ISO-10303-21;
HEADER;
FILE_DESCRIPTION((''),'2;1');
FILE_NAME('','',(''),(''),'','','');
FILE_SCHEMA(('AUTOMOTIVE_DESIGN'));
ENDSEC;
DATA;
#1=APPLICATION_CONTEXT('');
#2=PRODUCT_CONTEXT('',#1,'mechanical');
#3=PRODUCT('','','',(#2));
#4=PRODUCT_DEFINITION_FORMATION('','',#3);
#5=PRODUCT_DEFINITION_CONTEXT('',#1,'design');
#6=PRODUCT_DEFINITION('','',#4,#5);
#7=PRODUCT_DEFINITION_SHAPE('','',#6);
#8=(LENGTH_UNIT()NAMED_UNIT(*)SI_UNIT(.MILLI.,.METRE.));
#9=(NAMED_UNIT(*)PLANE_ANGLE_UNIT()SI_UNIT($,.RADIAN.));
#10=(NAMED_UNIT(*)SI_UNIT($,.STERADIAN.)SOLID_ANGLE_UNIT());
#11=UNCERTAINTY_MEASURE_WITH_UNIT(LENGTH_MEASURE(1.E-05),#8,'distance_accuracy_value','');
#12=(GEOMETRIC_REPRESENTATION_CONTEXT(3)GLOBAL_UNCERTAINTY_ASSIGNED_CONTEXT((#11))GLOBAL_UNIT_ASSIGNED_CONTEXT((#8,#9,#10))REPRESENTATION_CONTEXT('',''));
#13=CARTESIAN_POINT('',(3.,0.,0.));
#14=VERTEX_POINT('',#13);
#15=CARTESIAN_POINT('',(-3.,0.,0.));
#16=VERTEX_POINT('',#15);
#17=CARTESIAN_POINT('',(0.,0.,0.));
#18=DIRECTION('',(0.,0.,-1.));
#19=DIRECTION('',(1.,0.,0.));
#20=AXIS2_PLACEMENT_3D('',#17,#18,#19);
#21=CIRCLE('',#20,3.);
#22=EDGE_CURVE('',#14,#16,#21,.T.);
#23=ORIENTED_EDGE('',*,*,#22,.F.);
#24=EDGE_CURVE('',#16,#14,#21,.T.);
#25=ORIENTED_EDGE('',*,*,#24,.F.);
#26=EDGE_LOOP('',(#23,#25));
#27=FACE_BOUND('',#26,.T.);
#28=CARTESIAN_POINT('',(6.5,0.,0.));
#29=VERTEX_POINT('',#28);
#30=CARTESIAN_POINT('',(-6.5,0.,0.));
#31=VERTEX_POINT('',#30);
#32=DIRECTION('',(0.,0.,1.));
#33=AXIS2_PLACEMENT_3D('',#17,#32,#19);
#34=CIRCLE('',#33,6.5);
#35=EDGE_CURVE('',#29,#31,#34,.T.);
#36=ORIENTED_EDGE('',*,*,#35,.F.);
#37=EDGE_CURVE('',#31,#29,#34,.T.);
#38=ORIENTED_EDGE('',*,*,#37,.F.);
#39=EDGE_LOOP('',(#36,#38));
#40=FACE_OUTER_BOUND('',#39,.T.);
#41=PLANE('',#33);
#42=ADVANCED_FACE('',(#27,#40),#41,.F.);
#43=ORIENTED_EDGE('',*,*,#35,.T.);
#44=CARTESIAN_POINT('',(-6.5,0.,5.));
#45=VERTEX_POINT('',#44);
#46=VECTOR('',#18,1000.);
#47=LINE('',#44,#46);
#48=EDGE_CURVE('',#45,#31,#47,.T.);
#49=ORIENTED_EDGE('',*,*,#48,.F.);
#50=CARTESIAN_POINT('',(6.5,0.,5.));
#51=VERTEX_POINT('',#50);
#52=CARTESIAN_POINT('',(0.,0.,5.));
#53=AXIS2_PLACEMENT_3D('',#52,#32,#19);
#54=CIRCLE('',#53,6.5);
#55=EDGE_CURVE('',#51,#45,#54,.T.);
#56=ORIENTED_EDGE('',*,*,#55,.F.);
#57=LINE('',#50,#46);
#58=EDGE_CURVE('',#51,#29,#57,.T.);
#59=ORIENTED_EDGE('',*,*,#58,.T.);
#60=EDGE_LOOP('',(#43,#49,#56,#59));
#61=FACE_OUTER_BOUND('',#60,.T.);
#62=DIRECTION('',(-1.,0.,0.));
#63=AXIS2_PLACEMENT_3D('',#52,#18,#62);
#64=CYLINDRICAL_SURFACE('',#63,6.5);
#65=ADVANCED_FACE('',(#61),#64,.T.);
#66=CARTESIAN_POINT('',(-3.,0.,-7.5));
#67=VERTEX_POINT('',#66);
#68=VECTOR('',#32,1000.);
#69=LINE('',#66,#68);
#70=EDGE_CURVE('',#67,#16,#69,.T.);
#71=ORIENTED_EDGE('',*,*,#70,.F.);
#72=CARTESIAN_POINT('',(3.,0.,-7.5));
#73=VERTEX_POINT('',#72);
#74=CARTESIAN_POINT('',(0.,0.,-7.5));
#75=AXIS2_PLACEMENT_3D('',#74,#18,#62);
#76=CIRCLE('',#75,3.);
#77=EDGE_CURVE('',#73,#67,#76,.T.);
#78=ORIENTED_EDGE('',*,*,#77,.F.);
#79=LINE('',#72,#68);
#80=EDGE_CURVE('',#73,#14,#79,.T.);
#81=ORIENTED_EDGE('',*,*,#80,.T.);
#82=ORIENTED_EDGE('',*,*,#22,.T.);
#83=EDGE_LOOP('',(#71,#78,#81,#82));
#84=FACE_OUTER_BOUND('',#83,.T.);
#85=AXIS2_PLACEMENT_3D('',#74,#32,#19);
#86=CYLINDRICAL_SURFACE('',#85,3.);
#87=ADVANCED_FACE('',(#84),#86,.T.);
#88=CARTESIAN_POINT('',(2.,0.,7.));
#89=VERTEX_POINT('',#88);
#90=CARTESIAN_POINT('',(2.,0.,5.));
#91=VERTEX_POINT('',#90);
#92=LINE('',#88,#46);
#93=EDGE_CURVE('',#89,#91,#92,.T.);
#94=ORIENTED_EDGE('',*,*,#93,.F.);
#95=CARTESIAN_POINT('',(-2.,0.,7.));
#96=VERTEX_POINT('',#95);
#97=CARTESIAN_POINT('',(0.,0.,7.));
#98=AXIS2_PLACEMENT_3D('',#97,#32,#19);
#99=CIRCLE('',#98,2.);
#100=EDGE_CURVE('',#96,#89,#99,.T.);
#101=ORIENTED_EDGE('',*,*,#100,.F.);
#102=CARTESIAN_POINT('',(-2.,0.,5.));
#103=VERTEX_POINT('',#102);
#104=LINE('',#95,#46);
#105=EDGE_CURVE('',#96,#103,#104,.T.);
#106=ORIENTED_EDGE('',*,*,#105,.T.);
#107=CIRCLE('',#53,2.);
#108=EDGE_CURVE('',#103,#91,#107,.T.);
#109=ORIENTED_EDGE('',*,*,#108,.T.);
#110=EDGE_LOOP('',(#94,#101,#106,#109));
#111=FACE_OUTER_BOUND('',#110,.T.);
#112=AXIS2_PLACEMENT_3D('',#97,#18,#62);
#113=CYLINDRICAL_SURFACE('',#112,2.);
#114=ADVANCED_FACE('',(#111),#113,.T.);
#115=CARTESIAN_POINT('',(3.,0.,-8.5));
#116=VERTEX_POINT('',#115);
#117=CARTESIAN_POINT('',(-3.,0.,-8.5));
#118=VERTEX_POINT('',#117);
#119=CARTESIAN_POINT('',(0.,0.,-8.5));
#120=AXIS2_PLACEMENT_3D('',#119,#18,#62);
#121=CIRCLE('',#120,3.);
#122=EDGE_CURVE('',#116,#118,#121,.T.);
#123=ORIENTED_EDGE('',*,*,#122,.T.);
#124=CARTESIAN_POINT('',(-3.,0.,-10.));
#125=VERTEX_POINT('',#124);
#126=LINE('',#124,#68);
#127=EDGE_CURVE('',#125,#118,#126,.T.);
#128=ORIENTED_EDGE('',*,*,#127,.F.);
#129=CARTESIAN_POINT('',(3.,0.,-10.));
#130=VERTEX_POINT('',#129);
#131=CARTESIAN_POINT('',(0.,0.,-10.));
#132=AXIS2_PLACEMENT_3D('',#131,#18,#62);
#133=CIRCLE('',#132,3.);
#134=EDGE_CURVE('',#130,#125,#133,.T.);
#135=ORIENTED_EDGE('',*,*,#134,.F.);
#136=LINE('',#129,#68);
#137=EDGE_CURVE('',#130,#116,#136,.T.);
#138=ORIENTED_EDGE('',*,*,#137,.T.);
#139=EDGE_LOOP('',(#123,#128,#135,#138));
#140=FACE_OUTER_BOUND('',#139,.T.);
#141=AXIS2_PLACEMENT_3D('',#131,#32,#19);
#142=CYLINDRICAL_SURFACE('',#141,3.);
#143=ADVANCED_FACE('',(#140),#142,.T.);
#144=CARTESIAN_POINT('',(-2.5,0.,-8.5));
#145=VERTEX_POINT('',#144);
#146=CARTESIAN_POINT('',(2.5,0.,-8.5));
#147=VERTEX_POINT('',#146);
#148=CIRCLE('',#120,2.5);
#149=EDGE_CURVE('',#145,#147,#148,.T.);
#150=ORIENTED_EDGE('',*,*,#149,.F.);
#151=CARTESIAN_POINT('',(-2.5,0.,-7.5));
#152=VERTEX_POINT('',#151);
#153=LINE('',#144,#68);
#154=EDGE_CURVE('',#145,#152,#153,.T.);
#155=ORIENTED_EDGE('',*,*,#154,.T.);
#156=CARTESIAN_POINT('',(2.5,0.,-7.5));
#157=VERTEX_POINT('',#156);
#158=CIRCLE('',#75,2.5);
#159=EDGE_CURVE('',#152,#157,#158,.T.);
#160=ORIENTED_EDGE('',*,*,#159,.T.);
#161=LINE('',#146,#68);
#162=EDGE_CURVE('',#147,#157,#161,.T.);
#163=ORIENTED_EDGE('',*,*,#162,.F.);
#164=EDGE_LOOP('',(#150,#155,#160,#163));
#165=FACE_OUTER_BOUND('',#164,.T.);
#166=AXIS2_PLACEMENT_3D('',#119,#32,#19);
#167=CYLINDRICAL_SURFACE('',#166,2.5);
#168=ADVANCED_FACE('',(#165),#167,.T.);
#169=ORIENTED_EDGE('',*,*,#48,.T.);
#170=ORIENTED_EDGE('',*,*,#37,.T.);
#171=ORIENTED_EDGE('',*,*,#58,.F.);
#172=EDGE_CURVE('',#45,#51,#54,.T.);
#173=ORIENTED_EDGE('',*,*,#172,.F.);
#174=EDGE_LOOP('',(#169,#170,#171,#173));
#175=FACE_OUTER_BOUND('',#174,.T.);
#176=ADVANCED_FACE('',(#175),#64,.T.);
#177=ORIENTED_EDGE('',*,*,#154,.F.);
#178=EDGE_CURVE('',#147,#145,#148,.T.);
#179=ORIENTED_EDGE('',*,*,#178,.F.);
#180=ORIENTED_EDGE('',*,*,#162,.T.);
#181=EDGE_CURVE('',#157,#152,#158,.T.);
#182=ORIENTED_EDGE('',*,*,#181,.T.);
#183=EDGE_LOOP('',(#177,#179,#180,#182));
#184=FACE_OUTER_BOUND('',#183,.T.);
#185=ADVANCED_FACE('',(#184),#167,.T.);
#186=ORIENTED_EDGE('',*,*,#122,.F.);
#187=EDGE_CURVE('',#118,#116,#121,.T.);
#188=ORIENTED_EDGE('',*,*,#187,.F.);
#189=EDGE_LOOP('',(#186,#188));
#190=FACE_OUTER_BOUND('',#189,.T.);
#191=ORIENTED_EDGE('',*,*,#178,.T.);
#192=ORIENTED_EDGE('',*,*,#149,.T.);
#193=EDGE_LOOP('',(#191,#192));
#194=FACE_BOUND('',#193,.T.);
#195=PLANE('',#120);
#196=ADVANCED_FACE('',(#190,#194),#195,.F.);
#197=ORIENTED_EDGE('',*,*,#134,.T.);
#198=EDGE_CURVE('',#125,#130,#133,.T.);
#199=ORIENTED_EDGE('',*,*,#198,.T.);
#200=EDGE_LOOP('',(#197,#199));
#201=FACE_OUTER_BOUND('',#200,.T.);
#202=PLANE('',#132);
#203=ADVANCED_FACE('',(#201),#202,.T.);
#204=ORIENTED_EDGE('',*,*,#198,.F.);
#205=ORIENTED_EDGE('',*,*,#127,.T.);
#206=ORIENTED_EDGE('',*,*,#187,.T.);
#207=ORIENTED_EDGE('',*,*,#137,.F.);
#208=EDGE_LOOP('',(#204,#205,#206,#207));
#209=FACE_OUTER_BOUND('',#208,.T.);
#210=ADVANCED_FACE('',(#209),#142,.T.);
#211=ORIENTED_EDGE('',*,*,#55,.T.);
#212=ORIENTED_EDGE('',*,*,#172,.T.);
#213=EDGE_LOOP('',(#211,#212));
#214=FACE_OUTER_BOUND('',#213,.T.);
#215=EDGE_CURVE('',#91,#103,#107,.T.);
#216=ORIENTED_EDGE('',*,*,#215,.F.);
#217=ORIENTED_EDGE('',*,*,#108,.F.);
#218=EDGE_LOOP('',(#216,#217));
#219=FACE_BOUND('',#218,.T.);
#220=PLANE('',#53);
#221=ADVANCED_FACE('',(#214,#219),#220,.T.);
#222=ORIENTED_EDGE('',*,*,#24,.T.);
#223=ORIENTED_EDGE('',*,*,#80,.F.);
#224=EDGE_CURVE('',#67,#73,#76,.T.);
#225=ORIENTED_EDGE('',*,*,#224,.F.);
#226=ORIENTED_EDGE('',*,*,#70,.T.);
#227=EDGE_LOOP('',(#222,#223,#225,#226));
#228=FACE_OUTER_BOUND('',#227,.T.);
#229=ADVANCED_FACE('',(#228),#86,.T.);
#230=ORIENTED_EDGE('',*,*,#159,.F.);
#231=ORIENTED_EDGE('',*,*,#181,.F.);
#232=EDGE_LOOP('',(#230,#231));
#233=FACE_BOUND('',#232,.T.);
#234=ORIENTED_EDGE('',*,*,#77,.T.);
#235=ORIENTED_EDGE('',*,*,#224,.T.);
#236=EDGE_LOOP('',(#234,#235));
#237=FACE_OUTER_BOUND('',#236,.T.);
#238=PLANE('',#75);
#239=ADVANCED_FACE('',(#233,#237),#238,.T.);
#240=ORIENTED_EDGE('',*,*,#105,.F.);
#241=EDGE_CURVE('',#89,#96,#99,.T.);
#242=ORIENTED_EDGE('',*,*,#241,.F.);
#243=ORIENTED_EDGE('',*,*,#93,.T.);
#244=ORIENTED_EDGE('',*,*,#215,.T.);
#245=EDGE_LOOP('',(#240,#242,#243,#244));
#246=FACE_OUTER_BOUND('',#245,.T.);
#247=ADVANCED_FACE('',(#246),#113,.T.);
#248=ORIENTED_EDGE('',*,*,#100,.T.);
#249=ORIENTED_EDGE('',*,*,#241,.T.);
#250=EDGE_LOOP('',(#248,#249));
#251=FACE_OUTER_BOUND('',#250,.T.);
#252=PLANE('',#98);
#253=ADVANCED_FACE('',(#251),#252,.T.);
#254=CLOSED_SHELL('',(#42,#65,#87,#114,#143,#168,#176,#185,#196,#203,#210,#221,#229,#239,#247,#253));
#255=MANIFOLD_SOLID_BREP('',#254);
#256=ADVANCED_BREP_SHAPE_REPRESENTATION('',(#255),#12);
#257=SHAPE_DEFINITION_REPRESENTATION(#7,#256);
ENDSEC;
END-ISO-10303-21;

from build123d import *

# Parameters (mm, degrees)
SKETCH1_R      = 6.5
EXTRUDE1_DEPTH = 5
SKETCH2_R      = 2
EXTRUDE2_DEPTH = 2
SKETCH3_R      = 3
EXTRUDE3_DEPTH = 7.5
SKETCH4_R      = 2.5
EXTRUDE5_DEPTH = 1
SKETCH6_R      = 3
EXTRUDE6_DEPTH = 1.5


with BuildPart() as part:
    # Sketch1 → Extrude1 (new body)
    with BuildSketch(Plane.XY):
        Circle(SKETCH1_R)
    extrude(amount=EXTRUDE1_DEPTH)

    # Sketch2 → Extrude2 (add)
    with BuildSketch(Plane.XY.offset(5)):
        Circle(SKETCH2_R)
    extrude(amount=EXTRUDE2_DEPTH)

    # Sketch3 → Extrude3 (add)
    with BuildSketch(Plane(origin=(0, 0, 0), x_dir=(-1, 0, 0), z_dir=(0, 0, -1))):
        with Locations(Location((0, 0, 0), (0, 0, 180))):
            Circle(SKETCH3_R)
    extrude(amount=EXTRUDE3_DEPTH)

    # Sketch4 → Extrude5 (add)
    with BuildSketch(Plane(origin=(0, 0, -7.5), x_dir=(-1, 0, 0), z_dir=(0, 0, -1))):
        Circle(SKETCH4_R)
    extrude(amount=EXTRUDE5_DEPTH)

    # Sketch6 → Extrude6 (add)
    with BuildSketch(Plane(origin=(0, 0, -8.5), x_dir=(-1, 0, 0), z_dir=(0, 0, -1))):
        with Locations(Location((0, 0, 0), (0, 0, 180))):
            Circle(SKETCH6_R)
    extrude(amount=EXTRUDE6_DEPTH)


solid = part.part
